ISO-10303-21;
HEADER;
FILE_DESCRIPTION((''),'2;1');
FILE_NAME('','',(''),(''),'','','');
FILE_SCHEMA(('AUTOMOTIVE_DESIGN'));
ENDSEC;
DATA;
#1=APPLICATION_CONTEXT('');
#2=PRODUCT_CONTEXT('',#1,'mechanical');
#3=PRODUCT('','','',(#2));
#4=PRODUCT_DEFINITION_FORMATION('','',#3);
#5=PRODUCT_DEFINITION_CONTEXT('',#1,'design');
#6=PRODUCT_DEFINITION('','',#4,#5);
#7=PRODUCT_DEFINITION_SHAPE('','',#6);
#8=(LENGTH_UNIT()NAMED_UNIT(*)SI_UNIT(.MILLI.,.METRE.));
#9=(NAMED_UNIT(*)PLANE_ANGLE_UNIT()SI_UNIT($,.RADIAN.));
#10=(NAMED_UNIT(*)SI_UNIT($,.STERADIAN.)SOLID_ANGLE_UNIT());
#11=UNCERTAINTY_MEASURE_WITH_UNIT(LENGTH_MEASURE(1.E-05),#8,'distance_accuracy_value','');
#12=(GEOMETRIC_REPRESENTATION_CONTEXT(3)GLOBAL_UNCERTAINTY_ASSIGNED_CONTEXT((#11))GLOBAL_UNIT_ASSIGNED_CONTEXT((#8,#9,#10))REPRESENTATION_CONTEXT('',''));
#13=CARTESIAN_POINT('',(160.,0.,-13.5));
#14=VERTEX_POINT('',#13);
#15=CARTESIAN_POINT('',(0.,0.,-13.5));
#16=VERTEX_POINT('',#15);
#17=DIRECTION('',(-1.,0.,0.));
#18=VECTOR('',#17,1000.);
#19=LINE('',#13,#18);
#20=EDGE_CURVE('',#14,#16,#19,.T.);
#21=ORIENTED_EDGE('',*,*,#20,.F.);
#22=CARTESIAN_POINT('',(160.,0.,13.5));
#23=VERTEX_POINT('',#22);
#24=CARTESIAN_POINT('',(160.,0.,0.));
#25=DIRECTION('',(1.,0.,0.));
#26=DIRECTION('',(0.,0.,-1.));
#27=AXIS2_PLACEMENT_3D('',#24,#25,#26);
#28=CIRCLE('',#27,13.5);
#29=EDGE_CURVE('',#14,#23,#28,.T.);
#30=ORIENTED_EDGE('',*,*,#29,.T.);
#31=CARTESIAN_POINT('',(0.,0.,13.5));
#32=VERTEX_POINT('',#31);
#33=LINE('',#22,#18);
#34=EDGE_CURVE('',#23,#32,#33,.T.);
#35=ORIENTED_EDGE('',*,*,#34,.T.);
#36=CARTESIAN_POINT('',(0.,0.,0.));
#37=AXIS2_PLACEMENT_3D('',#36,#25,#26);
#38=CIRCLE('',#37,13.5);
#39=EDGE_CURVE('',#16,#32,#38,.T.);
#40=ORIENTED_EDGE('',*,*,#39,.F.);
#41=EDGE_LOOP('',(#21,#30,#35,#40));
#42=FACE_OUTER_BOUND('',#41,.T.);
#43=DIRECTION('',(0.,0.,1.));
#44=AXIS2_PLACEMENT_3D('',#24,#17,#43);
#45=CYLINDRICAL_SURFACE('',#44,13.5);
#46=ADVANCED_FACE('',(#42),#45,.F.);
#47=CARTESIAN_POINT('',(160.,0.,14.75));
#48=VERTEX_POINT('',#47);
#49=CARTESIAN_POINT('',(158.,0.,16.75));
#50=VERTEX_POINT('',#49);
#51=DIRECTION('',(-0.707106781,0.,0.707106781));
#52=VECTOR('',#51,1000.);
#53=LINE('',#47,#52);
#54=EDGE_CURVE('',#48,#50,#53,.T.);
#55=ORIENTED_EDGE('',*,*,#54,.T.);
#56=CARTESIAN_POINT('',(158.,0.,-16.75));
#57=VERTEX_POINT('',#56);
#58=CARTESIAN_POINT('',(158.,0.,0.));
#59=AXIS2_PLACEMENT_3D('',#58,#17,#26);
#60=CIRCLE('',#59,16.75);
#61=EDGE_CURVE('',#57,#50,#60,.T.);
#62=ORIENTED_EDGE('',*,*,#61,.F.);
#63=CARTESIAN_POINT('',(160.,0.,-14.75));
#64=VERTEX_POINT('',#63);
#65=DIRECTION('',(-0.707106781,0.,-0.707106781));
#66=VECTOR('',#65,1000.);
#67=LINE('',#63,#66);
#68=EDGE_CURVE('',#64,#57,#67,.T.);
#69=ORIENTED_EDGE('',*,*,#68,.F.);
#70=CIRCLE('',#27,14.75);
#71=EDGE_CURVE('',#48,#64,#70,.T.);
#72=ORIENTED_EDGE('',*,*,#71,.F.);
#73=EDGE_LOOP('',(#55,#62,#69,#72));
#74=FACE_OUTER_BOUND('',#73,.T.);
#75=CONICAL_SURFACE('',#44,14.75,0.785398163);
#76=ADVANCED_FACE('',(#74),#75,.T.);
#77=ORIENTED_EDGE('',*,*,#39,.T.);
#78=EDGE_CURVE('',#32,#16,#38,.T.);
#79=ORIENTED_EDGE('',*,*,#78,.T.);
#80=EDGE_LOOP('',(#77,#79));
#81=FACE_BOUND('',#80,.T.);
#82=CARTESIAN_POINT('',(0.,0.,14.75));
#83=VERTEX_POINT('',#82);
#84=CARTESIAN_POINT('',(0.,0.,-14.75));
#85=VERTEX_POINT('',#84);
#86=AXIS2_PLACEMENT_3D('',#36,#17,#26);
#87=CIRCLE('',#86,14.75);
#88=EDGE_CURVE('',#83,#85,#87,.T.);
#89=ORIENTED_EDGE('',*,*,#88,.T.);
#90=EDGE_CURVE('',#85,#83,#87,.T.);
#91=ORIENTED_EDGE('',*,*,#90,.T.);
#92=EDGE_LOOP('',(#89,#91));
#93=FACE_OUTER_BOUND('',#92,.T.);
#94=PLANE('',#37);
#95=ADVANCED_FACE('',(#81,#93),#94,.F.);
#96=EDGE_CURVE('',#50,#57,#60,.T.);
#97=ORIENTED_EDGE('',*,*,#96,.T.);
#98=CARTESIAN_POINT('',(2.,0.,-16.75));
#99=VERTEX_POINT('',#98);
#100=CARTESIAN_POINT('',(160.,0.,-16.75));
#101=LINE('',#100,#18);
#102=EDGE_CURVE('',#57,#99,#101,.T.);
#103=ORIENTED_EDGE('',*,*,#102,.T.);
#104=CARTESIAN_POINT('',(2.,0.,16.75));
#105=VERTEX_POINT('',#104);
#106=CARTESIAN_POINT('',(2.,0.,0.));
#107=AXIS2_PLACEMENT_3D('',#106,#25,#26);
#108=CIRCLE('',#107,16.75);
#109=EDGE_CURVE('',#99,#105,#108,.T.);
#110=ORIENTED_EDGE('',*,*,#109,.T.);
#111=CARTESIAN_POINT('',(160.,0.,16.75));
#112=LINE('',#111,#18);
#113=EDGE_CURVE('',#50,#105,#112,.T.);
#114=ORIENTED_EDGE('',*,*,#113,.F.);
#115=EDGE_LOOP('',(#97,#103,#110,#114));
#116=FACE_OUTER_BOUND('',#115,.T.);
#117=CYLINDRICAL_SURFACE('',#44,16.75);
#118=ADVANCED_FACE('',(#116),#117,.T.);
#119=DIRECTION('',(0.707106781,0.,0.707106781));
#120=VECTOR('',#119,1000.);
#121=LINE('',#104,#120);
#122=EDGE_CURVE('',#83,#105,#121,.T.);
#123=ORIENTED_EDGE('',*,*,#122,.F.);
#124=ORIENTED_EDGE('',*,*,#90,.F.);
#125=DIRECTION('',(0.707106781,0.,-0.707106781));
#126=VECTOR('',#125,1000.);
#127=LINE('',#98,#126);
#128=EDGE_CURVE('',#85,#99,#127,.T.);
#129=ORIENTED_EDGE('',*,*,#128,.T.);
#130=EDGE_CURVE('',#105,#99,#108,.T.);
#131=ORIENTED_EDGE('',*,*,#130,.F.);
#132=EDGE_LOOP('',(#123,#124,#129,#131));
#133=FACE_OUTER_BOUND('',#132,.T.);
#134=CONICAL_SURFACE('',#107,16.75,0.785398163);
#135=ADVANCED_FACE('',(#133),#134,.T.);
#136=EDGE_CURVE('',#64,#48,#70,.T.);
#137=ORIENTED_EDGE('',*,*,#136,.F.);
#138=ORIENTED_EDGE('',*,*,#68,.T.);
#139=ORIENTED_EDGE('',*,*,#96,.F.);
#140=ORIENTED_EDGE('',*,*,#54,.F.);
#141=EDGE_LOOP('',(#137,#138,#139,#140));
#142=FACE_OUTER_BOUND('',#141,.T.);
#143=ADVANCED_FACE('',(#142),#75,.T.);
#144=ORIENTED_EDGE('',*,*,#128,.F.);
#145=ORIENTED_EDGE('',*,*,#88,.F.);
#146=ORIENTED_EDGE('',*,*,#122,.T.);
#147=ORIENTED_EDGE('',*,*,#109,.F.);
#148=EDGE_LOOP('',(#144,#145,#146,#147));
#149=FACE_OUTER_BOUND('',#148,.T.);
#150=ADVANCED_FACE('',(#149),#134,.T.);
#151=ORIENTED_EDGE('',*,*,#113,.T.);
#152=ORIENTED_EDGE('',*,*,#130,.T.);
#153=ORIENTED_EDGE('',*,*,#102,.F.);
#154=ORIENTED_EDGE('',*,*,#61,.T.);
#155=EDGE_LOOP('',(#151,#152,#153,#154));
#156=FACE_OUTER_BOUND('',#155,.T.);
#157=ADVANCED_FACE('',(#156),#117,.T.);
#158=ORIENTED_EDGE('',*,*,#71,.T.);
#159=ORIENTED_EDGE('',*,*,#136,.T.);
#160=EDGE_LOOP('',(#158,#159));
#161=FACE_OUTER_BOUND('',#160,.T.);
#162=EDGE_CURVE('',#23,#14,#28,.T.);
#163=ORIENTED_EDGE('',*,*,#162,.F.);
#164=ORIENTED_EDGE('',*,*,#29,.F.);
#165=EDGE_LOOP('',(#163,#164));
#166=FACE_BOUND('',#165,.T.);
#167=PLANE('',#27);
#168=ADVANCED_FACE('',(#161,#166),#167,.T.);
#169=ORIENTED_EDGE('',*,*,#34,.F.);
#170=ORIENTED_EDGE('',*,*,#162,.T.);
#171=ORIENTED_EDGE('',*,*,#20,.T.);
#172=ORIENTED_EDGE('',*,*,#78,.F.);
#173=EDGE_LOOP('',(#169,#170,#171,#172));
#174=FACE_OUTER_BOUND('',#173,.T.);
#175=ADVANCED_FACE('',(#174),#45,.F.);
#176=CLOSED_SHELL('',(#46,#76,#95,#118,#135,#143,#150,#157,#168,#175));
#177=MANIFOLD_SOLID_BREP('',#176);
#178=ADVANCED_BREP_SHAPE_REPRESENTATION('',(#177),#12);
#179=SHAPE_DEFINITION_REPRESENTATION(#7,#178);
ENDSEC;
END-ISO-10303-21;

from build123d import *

# Parameters (mm, degrees)
SKETCH_1_R      = 16.75
SKETCH_1_R_2    = 13.5
EXTRUDE_1_DEPTH = 160
CHAMFER_1_SIZE  = 2


with BuildPart() as part:
    # 草图1 → 拉伸-薄壁1 (new body)
    with BuildSketch(Plane(origin=(0, 0, 0), x_dir=(0, 0, -1), z_dir=(1, 0, 0))):
        Circle(SKETCH_1_R)
        Circle(SKETCH_1_R_2, mode=Mode.SUBTRACT)
    extrude(amount=EXTRUDE_1_DEPTH)

    # 倒角1
    chamfer_1_edges = [part.edges().sort_by_distance(p)[0] for p in [
        (0, 0, 16.75),
        (160, 0, 16.75),
    ]]
    chamfer(chamfer_1_edges, length=CHAMFER_1_SIZE)


solid = part.part
